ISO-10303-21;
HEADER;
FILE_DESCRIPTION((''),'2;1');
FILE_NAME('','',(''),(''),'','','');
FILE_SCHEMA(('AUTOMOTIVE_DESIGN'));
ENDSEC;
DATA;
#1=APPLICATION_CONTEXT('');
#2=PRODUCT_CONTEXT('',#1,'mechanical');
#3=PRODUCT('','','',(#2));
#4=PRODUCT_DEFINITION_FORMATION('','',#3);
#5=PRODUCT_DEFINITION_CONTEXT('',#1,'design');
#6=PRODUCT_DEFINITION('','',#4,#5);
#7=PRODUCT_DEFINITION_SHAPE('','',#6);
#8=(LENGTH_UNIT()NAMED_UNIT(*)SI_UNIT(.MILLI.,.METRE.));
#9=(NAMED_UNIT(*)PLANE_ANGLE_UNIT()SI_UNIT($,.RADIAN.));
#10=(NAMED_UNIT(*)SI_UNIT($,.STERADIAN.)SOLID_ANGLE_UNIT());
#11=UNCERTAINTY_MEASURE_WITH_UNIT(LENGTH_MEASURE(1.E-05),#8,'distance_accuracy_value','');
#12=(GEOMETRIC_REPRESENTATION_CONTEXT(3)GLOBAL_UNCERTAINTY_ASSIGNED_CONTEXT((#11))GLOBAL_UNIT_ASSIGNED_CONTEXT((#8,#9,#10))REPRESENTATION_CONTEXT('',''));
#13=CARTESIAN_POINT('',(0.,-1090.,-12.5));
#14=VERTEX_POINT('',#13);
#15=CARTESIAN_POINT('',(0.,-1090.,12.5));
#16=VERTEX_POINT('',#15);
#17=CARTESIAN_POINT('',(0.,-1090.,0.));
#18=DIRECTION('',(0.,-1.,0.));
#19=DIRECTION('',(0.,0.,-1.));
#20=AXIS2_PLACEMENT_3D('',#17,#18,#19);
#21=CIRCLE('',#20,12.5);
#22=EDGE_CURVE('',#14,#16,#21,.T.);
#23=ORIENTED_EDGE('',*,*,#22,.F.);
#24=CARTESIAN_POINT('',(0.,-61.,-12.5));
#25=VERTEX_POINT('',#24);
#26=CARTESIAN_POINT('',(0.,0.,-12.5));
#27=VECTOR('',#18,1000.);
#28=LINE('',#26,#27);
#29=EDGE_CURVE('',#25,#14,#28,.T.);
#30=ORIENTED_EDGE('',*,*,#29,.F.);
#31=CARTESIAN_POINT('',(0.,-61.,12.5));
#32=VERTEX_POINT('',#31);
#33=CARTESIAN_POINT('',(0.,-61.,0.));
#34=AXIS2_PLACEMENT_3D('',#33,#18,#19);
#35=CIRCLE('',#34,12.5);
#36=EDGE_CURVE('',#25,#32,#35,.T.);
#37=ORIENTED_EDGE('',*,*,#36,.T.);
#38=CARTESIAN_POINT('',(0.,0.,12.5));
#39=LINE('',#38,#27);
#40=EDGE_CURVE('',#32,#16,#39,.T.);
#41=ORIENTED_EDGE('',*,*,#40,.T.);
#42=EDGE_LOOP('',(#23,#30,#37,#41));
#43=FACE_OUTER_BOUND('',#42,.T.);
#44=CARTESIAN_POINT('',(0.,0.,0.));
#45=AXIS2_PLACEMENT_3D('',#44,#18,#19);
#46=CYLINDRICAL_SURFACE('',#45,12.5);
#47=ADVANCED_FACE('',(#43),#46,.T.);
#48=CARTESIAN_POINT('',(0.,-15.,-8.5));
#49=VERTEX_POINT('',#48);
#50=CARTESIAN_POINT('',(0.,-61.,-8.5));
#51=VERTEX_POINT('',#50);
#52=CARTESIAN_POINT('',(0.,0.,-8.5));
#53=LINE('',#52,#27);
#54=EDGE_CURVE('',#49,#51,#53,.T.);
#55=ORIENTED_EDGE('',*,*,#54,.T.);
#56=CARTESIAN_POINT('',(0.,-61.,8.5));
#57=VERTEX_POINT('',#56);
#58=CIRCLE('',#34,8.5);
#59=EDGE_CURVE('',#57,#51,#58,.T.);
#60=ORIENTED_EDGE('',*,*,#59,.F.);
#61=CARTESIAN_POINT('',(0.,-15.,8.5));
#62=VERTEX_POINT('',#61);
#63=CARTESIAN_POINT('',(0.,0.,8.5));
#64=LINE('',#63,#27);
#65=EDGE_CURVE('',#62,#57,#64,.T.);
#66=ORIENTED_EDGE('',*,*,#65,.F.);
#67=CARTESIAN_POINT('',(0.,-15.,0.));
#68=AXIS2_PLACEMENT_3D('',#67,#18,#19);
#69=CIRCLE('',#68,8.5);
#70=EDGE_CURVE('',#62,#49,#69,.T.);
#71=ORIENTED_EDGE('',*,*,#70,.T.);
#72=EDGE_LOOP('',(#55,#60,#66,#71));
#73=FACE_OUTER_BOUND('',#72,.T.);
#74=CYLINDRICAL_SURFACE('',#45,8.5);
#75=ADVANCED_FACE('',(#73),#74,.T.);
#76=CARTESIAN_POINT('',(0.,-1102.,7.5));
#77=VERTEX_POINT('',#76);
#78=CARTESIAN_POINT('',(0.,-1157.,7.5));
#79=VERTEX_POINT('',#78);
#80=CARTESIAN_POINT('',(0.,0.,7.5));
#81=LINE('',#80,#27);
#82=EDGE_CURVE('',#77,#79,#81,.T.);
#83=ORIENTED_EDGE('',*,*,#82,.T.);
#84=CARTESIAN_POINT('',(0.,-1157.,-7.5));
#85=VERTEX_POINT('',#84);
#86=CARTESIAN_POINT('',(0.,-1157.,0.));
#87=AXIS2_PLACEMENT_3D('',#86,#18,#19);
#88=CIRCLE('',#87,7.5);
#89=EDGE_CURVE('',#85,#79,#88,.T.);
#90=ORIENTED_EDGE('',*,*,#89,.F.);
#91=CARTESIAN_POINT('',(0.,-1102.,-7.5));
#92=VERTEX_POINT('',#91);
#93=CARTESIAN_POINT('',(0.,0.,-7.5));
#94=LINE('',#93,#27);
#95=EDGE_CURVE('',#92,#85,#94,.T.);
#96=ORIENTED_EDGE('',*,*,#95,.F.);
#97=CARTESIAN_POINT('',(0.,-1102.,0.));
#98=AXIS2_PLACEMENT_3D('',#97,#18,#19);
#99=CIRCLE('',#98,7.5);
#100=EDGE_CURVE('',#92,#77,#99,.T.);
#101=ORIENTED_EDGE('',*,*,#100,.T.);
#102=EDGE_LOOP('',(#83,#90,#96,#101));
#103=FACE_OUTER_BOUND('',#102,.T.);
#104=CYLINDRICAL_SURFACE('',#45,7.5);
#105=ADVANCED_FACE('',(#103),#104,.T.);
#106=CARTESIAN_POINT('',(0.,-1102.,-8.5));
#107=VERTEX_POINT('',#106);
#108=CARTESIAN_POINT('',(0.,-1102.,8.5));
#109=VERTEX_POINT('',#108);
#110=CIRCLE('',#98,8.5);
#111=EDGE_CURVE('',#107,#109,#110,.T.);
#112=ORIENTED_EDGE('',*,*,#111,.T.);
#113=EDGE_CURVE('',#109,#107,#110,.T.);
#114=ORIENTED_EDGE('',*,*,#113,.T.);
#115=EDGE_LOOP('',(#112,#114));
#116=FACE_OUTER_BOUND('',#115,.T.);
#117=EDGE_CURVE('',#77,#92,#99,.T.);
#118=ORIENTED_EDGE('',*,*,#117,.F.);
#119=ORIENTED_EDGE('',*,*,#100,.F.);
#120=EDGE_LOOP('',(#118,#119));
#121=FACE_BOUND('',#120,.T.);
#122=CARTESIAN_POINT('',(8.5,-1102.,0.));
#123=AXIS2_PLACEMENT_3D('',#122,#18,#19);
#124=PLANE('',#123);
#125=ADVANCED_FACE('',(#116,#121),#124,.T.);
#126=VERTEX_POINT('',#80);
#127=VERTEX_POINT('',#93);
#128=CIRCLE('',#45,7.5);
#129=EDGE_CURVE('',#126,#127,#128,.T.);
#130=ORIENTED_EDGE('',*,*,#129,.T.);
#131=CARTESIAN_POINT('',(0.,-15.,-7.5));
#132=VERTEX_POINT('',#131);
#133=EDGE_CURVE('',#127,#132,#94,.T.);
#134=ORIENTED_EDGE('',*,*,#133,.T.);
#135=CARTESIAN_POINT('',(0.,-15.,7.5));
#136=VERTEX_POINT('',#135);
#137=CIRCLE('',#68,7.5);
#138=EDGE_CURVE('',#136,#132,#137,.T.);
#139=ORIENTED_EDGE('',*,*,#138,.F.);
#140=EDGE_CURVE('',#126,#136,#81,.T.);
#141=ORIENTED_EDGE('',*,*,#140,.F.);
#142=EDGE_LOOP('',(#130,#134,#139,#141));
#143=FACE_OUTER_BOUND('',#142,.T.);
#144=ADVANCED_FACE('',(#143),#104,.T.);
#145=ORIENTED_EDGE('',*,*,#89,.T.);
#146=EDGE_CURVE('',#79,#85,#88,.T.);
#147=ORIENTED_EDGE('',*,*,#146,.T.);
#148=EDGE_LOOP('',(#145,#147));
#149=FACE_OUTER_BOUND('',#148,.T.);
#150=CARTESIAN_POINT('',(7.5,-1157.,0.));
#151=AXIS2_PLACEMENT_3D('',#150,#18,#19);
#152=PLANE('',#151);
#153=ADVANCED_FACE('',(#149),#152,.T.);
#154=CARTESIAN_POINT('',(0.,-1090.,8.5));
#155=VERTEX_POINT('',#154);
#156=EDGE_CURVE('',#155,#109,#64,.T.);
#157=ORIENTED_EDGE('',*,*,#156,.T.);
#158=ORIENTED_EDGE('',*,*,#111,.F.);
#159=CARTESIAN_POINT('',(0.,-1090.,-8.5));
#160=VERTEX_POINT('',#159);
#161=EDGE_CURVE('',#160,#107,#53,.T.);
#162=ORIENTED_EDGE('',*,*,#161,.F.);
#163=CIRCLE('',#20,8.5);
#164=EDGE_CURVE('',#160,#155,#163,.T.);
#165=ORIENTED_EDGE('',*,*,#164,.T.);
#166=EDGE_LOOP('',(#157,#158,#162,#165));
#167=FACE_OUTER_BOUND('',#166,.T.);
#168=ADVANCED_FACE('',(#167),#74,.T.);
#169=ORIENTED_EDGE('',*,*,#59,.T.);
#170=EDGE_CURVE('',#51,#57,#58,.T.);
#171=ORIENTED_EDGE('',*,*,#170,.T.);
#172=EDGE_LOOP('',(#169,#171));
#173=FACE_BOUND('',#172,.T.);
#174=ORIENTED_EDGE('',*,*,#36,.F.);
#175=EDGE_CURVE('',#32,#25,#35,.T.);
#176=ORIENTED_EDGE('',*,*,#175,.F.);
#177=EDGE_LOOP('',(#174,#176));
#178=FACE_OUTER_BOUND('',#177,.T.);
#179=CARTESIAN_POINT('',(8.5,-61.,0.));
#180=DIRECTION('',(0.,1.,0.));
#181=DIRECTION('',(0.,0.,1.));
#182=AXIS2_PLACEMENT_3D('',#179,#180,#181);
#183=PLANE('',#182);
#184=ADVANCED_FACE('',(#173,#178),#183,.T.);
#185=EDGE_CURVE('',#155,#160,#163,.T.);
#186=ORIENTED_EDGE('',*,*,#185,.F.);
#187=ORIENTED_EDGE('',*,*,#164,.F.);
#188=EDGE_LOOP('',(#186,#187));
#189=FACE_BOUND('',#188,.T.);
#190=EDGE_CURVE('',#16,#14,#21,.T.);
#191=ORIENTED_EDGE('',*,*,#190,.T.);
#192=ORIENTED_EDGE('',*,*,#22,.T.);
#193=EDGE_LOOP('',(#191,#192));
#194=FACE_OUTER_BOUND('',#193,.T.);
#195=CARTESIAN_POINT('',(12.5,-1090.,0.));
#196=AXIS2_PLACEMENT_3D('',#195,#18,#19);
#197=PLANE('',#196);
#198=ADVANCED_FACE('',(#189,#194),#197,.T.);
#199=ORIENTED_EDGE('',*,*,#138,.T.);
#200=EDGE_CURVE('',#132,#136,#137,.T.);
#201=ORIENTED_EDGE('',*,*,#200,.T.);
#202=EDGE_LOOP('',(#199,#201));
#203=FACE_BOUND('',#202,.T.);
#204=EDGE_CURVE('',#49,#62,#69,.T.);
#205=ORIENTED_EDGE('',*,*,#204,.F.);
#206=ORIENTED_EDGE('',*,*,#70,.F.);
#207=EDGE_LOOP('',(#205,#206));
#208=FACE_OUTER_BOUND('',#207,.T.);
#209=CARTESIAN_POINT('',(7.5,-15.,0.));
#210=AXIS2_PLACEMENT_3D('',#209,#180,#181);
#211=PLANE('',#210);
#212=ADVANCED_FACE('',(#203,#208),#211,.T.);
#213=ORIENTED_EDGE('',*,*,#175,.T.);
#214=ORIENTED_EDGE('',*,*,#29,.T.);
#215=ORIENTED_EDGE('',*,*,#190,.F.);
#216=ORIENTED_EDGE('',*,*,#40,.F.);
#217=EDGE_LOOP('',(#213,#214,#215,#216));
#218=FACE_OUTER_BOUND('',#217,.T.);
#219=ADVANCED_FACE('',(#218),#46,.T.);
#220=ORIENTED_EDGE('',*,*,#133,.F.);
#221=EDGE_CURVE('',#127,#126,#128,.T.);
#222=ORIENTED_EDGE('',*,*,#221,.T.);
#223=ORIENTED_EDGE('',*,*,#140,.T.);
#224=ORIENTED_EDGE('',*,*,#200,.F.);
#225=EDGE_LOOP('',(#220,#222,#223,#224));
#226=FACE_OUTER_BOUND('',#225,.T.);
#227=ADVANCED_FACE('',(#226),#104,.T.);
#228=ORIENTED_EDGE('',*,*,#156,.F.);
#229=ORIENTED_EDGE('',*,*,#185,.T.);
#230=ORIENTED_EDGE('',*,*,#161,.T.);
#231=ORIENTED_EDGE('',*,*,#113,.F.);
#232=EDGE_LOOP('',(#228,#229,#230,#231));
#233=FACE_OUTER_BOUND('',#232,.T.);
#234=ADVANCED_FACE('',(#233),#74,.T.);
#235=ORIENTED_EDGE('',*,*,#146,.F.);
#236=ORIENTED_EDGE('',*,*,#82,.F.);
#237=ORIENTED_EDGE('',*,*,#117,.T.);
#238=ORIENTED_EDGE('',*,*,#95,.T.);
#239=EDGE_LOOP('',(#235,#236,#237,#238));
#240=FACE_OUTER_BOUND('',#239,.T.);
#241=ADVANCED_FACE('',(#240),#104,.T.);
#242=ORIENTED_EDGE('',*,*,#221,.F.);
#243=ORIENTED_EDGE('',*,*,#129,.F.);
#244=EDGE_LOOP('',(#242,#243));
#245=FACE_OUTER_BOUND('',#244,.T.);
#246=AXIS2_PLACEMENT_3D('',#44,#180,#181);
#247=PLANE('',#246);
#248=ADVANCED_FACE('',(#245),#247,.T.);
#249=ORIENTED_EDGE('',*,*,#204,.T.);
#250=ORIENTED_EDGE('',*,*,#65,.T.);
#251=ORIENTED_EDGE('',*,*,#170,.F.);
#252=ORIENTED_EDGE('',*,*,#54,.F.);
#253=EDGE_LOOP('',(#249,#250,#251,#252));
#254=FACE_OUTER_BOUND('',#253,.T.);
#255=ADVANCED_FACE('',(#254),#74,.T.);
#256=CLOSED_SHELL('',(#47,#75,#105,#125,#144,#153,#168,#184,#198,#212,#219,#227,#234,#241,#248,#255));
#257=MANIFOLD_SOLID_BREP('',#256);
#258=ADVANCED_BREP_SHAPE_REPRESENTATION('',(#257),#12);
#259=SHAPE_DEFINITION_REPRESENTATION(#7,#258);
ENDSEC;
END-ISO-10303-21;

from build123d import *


with BuildPart() as part:
    # Sketch2 → Revolve1 (revolve)
    with BuildSketch(Plane.XY, mode=Mode.PRIVATE) as revolve1_sk:
        Polygon((0, 0), (7.5, 0), (7.5, -15), (8.5, -15), (8.5, -61), (12.5, -61), (12.5, -1090), (8.5, -1090), (8.5, -1102), (7.5, -1102), (7.5, -1157), (0, -1157), align=None)
    revolve(revolve1_sk.sketch.rotate(Axis((0, 0, 0), (0, 1, 0)), 90), axis=Axis((0, 0, 0), (0, 1, 0)))


solid = part.part
